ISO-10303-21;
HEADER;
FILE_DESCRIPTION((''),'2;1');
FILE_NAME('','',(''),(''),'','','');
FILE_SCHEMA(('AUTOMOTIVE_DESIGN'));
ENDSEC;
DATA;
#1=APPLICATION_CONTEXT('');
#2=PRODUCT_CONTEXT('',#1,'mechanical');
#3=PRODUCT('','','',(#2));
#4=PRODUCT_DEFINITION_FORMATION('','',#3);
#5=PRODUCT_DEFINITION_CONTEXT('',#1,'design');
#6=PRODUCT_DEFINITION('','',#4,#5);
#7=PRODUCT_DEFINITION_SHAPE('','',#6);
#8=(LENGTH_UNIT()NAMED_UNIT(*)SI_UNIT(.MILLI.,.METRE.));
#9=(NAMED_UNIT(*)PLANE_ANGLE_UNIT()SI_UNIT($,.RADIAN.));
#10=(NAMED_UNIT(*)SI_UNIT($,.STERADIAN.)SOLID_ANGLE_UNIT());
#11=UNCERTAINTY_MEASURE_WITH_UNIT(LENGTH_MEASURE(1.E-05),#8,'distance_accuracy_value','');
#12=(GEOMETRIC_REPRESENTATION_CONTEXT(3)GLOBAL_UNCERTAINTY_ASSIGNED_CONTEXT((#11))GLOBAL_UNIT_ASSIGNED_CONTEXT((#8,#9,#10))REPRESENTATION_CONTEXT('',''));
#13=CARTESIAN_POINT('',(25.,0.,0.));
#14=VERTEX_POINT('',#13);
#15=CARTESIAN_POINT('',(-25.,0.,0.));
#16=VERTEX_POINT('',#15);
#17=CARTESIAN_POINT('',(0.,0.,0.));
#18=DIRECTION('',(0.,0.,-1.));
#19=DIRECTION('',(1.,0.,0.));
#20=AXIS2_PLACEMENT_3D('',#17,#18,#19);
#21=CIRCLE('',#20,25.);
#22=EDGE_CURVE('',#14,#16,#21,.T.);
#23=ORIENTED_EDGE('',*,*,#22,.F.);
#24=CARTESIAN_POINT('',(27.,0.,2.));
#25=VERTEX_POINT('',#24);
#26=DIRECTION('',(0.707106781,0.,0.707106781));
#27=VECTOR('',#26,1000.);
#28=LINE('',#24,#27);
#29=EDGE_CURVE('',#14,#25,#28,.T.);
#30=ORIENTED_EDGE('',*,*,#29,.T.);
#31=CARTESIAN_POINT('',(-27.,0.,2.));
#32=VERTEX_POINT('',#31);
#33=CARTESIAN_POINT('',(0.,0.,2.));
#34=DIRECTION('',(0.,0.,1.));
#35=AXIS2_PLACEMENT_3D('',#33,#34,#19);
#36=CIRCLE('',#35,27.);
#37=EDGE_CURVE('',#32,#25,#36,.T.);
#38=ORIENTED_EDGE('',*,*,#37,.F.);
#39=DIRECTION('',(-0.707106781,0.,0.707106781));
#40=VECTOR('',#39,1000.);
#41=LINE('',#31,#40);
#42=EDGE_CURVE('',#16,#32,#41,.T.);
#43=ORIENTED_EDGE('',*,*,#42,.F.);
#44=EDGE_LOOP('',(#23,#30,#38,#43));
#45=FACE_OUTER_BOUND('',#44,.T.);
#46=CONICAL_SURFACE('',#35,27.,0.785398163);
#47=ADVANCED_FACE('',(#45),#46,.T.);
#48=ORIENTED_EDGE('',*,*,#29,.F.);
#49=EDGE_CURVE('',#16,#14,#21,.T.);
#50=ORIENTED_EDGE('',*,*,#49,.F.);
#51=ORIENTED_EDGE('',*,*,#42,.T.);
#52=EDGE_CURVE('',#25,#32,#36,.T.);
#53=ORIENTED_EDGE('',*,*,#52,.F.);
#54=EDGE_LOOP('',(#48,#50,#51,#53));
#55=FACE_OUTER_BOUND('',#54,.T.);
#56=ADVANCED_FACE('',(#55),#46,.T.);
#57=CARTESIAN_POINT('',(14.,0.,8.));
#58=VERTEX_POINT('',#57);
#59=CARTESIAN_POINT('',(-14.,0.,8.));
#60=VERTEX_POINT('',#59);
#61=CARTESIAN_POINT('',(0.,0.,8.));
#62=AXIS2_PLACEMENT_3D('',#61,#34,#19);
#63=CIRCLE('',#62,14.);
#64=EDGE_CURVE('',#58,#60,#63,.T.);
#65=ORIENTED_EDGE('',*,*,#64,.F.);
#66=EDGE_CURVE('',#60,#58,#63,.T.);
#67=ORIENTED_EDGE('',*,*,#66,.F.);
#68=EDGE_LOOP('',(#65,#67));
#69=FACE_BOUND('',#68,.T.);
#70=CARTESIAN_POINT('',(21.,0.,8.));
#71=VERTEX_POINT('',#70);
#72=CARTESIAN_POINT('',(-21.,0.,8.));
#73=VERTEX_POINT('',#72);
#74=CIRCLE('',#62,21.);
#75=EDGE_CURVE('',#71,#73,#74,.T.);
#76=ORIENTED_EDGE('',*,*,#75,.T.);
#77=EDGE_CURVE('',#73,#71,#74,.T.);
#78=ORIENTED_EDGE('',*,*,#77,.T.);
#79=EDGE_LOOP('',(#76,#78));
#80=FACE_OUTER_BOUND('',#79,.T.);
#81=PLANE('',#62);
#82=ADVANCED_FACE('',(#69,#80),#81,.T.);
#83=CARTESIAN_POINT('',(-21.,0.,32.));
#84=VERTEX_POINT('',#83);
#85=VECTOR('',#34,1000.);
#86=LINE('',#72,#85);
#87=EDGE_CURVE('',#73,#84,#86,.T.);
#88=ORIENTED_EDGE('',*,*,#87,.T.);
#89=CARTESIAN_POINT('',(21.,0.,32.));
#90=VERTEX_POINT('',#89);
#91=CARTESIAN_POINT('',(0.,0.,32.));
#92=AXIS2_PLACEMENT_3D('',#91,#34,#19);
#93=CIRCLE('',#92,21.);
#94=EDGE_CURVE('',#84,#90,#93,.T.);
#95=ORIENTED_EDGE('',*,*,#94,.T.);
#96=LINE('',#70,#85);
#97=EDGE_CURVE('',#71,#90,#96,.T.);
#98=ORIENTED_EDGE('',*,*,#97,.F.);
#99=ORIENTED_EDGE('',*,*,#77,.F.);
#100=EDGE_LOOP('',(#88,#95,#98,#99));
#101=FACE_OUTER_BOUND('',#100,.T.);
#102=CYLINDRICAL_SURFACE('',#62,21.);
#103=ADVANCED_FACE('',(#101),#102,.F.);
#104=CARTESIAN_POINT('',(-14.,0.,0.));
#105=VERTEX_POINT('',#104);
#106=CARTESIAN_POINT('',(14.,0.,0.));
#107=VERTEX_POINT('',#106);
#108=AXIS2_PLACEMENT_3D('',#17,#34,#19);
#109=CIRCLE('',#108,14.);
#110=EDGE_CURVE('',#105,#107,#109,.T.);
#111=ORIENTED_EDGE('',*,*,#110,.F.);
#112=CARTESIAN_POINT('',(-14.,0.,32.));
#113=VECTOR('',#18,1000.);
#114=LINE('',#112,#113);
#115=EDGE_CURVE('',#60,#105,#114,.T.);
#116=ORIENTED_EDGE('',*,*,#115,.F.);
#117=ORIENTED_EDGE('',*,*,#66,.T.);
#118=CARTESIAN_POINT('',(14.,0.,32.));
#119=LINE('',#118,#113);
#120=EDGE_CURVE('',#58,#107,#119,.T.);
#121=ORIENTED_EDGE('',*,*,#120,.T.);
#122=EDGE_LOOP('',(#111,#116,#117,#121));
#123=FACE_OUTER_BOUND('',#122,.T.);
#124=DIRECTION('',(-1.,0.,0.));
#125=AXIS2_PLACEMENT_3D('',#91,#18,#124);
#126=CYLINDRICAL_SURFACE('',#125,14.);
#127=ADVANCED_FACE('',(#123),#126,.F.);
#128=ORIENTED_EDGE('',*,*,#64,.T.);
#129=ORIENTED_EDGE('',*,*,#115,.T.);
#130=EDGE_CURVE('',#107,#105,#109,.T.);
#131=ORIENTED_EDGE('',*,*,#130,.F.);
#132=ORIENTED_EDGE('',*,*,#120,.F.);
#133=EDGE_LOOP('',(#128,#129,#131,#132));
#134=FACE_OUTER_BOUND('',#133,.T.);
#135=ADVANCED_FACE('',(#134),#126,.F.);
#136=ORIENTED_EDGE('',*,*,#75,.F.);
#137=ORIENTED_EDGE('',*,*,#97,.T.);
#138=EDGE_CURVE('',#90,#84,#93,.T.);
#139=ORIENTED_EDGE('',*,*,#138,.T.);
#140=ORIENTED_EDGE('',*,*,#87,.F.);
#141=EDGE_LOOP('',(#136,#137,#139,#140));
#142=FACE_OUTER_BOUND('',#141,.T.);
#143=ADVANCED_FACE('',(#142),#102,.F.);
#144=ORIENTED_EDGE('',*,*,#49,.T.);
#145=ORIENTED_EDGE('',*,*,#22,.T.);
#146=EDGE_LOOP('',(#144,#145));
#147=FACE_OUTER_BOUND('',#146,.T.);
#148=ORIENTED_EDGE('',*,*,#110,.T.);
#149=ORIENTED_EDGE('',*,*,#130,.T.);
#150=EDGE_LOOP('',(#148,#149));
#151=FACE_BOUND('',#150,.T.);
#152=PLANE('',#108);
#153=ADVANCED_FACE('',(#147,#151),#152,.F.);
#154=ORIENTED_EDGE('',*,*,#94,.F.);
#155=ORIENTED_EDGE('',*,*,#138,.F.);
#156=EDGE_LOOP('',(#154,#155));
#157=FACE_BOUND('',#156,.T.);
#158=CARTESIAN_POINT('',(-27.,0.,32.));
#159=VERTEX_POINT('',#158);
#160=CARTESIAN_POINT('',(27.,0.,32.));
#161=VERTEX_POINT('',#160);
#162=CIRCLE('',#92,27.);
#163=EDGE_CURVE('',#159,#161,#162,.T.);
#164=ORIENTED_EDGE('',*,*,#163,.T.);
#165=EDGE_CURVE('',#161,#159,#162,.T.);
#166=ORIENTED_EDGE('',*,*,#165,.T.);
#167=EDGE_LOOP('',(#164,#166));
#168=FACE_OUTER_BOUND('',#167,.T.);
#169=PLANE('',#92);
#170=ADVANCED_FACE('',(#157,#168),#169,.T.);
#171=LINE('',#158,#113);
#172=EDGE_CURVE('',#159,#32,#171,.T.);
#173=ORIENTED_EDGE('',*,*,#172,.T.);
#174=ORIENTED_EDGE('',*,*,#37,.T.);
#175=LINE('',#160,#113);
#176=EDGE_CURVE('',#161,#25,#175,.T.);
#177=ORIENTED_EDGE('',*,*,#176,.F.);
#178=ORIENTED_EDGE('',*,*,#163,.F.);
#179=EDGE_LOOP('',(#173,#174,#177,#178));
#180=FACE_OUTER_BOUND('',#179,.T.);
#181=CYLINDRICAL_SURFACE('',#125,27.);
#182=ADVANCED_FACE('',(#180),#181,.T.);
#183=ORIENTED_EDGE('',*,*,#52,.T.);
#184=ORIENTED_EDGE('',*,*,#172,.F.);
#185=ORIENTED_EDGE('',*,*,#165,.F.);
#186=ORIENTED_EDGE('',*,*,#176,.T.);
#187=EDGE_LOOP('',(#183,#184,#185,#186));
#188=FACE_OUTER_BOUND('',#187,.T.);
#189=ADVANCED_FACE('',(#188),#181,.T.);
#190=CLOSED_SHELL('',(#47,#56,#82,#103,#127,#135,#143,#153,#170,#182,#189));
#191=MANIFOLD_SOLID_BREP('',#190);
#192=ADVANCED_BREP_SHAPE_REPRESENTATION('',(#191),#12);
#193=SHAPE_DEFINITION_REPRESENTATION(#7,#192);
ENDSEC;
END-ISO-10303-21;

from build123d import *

# Parameters (mm, degrees)
SKETCH1_R           = 27
SKETCH1_R_2         = 14
BOSS_EXTRUDE1_DEPTH = 32
SKETCH2_R           = 21
CUT_EXTRUDE1_DEPTH  = 24
CHAMFER1_SIZE       = 2


with BuildPart() as part:
    # Sketch1 → Boss-Extrude1 (new body)
    with BuildSketch(Plane.XY):
        Circle(SKETCH1_R)
        Circle(SKETCH1_R_2, mode=Mode.SUBTRACT)
    extrude(amount=BOSS_EXTRUDE1_DEPTH)

    # Sketch2 → Cut-Extrude1 (cut)
    with BuildSketch(Plane.XY.offset(32)):
        Circle(SKETCH2_R)
    extrude(amount=-CUT_EXTRUDE1_DEPTH, mode=Mode.SUBTRACT)

    # Chamfer1
    chamfer1_edges = [part.edges().sort_by_distance(p)[0] for p in [
        (-27, 0, 0),
    ]]
    chamfer(chamfer1_edges, length=CHAMFER1_SIZE)


solid = part.part
